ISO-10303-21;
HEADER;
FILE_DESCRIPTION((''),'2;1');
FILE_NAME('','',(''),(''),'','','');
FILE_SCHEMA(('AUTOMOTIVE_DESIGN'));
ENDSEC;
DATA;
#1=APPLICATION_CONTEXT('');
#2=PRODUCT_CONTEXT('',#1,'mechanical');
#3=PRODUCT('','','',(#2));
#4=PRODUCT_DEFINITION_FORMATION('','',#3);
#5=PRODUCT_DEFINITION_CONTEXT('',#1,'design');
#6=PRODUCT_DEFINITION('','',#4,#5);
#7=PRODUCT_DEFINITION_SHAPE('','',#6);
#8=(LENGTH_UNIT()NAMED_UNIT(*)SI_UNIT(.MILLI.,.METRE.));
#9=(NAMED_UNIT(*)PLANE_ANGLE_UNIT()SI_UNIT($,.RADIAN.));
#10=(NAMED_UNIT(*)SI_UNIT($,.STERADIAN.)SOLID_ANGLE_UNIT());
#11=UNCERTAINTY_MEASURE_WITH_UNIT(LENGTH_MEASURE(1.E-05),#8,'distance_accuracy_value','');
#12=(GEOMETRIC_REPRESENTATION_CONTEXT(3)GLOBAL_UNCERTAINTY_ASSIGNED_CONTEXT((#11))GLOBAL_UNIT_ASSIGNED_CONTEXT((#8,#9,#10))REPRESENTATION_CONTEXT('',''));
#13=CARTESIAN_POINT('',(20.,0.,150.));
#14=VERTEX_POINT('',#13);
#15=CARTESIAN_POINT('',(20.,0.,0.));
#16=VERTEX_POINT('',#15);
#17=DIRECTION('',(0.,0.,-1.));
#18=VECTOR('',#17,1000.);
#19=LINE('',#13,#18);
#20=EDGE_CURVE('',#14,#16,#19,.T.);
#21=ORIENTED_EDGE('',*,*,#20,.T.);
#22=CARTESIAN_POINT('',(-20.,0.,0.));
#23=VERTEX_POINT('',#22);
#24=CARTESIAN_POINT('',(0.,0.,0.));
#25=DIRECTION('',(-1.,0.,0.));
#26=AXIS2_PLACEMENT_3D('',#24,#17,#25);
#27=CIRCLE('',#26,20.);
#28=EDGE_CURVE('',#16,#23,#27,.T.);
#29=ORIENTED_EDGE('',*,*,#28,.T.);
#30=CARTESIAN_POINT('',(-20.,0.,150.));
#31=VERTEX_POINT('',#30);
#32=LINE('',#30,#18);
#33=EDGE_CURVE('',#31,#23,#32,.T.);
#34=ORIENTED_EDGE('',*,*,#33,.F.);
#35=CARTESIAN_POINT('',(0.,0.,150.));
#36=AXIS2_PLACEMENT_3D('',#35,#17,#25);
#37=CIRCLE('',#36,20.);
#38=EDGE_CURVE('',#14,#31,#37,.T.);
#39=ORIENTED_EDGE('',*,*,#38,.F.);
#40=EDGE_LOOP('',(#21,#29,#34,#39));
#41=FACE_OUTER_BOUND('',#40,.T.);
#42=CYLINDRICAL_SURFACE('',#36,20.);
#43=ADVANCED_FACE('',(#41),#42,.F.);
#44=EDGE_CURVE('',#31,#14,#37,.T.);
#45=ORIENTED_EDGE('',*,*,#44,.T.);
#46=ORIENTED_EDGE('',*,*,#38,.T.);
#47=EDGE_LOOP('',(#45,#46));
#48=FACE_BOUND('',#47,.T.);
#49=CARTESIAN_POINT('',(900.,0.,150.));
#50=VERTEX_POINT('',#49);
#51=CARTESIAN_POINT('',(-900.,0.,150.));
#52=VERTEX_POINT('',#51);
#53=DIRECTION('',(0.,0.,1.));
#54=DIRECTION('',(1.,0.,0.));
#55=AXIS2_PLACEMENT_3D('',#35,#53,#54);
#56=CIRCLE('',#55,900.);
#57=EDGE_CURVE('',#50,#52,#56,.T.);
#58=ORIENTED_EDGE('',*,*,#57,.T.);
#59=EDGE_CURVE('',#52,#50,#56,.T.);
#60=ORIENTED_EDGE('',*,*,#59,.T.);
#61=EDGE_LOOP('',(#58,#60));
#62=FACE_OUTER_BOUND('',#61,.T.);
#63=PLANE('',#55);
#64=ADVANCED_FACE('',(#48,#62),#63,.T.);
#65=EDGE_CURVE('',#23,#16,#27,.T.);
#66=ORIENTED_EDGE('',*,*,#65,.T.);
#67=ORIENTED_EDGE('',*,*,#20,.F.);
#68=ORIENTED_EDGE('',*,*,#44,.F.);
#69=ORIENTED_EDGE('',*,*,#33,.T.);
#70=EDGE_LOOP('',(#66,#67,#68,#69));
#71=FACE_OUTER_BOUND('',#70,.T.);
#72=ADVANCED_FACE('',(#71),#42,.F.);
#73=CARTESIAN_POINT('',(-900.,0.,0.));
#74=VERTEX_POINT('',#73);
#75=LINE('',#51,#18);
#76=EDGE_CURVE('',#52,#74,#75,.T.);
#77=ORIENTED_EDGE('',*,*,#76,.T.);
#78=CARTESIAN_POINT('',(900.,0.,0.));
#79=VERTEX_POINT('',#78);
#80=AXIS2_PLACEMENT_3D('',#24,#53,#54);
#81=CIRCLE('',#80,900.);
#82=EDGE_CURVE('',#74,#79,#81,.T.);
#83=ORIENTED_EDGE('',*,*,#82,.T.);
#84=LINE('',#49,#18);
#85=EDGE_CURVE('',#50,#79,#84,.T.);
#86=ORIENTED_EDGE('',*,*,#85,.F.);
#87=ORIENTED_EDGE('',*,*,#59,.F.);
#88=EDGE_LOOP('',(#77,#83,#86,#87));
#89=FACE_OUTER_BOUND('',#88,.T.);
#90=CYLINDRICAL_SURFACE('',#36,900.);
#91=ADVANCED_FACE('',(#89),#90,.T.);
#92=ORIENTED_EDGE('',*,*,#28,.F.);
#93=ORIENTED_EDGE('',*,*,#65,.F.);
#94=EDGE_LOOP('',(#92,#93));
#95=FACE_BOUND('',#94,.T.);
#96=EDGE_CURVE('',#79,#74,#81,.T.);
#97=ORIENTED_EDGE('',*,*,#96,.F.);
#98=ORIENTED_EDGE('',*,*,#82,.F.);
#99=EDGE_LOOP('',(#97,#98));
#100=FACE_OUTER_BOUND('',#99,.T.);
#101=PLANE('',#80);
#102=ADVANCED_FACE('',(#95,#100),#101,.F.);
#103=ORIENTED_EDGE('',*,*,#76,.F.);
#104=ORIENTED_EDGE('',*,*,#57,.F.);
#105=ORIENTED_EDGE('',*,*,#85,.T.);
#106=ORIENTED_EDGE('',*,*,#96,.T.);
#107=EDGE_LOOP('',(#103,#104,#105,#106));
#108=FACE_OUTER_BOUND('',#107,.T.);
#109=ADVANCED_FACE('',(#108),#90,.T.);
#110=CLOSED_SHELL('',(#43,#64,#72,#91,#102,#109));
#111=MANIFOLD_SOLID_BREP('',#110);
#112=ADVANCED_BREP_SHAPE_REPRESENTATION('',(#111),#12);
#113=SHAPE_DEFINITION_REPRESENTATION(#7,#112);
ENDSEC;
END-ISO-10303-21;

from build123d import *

# Parameters (mm, degrees)
SKETCH1_R           = 900
BOSS_EXTRUDE1_DEPTH = 150
SKETCH2_R           = 20
CUT_EXTRUDE1_DEPTH  = 1282.600561798


with BuildPart() as part:
    # Sketch1 → Boss-Extrude1 (new body)
    with BuildSketch(Plane.XY):
        Circle(SKETCH1_R)
    extrude(amount=BOSS_EXTRUDE1_DEPTH)

    # Sketch2 → Cut-Extrude1 (cut, through all)
    with BuildSketch(Plane(origin=(0, 0, 0), x_dir=(-1, 0, 0), z_dir=(0, 0, -1))):
        Circle(SKETCH2_R)
    extrude(amount=-CUT_EXTRUDE1_DEPTH, mode=Mode.SUBTRACT)


solid = part.part
